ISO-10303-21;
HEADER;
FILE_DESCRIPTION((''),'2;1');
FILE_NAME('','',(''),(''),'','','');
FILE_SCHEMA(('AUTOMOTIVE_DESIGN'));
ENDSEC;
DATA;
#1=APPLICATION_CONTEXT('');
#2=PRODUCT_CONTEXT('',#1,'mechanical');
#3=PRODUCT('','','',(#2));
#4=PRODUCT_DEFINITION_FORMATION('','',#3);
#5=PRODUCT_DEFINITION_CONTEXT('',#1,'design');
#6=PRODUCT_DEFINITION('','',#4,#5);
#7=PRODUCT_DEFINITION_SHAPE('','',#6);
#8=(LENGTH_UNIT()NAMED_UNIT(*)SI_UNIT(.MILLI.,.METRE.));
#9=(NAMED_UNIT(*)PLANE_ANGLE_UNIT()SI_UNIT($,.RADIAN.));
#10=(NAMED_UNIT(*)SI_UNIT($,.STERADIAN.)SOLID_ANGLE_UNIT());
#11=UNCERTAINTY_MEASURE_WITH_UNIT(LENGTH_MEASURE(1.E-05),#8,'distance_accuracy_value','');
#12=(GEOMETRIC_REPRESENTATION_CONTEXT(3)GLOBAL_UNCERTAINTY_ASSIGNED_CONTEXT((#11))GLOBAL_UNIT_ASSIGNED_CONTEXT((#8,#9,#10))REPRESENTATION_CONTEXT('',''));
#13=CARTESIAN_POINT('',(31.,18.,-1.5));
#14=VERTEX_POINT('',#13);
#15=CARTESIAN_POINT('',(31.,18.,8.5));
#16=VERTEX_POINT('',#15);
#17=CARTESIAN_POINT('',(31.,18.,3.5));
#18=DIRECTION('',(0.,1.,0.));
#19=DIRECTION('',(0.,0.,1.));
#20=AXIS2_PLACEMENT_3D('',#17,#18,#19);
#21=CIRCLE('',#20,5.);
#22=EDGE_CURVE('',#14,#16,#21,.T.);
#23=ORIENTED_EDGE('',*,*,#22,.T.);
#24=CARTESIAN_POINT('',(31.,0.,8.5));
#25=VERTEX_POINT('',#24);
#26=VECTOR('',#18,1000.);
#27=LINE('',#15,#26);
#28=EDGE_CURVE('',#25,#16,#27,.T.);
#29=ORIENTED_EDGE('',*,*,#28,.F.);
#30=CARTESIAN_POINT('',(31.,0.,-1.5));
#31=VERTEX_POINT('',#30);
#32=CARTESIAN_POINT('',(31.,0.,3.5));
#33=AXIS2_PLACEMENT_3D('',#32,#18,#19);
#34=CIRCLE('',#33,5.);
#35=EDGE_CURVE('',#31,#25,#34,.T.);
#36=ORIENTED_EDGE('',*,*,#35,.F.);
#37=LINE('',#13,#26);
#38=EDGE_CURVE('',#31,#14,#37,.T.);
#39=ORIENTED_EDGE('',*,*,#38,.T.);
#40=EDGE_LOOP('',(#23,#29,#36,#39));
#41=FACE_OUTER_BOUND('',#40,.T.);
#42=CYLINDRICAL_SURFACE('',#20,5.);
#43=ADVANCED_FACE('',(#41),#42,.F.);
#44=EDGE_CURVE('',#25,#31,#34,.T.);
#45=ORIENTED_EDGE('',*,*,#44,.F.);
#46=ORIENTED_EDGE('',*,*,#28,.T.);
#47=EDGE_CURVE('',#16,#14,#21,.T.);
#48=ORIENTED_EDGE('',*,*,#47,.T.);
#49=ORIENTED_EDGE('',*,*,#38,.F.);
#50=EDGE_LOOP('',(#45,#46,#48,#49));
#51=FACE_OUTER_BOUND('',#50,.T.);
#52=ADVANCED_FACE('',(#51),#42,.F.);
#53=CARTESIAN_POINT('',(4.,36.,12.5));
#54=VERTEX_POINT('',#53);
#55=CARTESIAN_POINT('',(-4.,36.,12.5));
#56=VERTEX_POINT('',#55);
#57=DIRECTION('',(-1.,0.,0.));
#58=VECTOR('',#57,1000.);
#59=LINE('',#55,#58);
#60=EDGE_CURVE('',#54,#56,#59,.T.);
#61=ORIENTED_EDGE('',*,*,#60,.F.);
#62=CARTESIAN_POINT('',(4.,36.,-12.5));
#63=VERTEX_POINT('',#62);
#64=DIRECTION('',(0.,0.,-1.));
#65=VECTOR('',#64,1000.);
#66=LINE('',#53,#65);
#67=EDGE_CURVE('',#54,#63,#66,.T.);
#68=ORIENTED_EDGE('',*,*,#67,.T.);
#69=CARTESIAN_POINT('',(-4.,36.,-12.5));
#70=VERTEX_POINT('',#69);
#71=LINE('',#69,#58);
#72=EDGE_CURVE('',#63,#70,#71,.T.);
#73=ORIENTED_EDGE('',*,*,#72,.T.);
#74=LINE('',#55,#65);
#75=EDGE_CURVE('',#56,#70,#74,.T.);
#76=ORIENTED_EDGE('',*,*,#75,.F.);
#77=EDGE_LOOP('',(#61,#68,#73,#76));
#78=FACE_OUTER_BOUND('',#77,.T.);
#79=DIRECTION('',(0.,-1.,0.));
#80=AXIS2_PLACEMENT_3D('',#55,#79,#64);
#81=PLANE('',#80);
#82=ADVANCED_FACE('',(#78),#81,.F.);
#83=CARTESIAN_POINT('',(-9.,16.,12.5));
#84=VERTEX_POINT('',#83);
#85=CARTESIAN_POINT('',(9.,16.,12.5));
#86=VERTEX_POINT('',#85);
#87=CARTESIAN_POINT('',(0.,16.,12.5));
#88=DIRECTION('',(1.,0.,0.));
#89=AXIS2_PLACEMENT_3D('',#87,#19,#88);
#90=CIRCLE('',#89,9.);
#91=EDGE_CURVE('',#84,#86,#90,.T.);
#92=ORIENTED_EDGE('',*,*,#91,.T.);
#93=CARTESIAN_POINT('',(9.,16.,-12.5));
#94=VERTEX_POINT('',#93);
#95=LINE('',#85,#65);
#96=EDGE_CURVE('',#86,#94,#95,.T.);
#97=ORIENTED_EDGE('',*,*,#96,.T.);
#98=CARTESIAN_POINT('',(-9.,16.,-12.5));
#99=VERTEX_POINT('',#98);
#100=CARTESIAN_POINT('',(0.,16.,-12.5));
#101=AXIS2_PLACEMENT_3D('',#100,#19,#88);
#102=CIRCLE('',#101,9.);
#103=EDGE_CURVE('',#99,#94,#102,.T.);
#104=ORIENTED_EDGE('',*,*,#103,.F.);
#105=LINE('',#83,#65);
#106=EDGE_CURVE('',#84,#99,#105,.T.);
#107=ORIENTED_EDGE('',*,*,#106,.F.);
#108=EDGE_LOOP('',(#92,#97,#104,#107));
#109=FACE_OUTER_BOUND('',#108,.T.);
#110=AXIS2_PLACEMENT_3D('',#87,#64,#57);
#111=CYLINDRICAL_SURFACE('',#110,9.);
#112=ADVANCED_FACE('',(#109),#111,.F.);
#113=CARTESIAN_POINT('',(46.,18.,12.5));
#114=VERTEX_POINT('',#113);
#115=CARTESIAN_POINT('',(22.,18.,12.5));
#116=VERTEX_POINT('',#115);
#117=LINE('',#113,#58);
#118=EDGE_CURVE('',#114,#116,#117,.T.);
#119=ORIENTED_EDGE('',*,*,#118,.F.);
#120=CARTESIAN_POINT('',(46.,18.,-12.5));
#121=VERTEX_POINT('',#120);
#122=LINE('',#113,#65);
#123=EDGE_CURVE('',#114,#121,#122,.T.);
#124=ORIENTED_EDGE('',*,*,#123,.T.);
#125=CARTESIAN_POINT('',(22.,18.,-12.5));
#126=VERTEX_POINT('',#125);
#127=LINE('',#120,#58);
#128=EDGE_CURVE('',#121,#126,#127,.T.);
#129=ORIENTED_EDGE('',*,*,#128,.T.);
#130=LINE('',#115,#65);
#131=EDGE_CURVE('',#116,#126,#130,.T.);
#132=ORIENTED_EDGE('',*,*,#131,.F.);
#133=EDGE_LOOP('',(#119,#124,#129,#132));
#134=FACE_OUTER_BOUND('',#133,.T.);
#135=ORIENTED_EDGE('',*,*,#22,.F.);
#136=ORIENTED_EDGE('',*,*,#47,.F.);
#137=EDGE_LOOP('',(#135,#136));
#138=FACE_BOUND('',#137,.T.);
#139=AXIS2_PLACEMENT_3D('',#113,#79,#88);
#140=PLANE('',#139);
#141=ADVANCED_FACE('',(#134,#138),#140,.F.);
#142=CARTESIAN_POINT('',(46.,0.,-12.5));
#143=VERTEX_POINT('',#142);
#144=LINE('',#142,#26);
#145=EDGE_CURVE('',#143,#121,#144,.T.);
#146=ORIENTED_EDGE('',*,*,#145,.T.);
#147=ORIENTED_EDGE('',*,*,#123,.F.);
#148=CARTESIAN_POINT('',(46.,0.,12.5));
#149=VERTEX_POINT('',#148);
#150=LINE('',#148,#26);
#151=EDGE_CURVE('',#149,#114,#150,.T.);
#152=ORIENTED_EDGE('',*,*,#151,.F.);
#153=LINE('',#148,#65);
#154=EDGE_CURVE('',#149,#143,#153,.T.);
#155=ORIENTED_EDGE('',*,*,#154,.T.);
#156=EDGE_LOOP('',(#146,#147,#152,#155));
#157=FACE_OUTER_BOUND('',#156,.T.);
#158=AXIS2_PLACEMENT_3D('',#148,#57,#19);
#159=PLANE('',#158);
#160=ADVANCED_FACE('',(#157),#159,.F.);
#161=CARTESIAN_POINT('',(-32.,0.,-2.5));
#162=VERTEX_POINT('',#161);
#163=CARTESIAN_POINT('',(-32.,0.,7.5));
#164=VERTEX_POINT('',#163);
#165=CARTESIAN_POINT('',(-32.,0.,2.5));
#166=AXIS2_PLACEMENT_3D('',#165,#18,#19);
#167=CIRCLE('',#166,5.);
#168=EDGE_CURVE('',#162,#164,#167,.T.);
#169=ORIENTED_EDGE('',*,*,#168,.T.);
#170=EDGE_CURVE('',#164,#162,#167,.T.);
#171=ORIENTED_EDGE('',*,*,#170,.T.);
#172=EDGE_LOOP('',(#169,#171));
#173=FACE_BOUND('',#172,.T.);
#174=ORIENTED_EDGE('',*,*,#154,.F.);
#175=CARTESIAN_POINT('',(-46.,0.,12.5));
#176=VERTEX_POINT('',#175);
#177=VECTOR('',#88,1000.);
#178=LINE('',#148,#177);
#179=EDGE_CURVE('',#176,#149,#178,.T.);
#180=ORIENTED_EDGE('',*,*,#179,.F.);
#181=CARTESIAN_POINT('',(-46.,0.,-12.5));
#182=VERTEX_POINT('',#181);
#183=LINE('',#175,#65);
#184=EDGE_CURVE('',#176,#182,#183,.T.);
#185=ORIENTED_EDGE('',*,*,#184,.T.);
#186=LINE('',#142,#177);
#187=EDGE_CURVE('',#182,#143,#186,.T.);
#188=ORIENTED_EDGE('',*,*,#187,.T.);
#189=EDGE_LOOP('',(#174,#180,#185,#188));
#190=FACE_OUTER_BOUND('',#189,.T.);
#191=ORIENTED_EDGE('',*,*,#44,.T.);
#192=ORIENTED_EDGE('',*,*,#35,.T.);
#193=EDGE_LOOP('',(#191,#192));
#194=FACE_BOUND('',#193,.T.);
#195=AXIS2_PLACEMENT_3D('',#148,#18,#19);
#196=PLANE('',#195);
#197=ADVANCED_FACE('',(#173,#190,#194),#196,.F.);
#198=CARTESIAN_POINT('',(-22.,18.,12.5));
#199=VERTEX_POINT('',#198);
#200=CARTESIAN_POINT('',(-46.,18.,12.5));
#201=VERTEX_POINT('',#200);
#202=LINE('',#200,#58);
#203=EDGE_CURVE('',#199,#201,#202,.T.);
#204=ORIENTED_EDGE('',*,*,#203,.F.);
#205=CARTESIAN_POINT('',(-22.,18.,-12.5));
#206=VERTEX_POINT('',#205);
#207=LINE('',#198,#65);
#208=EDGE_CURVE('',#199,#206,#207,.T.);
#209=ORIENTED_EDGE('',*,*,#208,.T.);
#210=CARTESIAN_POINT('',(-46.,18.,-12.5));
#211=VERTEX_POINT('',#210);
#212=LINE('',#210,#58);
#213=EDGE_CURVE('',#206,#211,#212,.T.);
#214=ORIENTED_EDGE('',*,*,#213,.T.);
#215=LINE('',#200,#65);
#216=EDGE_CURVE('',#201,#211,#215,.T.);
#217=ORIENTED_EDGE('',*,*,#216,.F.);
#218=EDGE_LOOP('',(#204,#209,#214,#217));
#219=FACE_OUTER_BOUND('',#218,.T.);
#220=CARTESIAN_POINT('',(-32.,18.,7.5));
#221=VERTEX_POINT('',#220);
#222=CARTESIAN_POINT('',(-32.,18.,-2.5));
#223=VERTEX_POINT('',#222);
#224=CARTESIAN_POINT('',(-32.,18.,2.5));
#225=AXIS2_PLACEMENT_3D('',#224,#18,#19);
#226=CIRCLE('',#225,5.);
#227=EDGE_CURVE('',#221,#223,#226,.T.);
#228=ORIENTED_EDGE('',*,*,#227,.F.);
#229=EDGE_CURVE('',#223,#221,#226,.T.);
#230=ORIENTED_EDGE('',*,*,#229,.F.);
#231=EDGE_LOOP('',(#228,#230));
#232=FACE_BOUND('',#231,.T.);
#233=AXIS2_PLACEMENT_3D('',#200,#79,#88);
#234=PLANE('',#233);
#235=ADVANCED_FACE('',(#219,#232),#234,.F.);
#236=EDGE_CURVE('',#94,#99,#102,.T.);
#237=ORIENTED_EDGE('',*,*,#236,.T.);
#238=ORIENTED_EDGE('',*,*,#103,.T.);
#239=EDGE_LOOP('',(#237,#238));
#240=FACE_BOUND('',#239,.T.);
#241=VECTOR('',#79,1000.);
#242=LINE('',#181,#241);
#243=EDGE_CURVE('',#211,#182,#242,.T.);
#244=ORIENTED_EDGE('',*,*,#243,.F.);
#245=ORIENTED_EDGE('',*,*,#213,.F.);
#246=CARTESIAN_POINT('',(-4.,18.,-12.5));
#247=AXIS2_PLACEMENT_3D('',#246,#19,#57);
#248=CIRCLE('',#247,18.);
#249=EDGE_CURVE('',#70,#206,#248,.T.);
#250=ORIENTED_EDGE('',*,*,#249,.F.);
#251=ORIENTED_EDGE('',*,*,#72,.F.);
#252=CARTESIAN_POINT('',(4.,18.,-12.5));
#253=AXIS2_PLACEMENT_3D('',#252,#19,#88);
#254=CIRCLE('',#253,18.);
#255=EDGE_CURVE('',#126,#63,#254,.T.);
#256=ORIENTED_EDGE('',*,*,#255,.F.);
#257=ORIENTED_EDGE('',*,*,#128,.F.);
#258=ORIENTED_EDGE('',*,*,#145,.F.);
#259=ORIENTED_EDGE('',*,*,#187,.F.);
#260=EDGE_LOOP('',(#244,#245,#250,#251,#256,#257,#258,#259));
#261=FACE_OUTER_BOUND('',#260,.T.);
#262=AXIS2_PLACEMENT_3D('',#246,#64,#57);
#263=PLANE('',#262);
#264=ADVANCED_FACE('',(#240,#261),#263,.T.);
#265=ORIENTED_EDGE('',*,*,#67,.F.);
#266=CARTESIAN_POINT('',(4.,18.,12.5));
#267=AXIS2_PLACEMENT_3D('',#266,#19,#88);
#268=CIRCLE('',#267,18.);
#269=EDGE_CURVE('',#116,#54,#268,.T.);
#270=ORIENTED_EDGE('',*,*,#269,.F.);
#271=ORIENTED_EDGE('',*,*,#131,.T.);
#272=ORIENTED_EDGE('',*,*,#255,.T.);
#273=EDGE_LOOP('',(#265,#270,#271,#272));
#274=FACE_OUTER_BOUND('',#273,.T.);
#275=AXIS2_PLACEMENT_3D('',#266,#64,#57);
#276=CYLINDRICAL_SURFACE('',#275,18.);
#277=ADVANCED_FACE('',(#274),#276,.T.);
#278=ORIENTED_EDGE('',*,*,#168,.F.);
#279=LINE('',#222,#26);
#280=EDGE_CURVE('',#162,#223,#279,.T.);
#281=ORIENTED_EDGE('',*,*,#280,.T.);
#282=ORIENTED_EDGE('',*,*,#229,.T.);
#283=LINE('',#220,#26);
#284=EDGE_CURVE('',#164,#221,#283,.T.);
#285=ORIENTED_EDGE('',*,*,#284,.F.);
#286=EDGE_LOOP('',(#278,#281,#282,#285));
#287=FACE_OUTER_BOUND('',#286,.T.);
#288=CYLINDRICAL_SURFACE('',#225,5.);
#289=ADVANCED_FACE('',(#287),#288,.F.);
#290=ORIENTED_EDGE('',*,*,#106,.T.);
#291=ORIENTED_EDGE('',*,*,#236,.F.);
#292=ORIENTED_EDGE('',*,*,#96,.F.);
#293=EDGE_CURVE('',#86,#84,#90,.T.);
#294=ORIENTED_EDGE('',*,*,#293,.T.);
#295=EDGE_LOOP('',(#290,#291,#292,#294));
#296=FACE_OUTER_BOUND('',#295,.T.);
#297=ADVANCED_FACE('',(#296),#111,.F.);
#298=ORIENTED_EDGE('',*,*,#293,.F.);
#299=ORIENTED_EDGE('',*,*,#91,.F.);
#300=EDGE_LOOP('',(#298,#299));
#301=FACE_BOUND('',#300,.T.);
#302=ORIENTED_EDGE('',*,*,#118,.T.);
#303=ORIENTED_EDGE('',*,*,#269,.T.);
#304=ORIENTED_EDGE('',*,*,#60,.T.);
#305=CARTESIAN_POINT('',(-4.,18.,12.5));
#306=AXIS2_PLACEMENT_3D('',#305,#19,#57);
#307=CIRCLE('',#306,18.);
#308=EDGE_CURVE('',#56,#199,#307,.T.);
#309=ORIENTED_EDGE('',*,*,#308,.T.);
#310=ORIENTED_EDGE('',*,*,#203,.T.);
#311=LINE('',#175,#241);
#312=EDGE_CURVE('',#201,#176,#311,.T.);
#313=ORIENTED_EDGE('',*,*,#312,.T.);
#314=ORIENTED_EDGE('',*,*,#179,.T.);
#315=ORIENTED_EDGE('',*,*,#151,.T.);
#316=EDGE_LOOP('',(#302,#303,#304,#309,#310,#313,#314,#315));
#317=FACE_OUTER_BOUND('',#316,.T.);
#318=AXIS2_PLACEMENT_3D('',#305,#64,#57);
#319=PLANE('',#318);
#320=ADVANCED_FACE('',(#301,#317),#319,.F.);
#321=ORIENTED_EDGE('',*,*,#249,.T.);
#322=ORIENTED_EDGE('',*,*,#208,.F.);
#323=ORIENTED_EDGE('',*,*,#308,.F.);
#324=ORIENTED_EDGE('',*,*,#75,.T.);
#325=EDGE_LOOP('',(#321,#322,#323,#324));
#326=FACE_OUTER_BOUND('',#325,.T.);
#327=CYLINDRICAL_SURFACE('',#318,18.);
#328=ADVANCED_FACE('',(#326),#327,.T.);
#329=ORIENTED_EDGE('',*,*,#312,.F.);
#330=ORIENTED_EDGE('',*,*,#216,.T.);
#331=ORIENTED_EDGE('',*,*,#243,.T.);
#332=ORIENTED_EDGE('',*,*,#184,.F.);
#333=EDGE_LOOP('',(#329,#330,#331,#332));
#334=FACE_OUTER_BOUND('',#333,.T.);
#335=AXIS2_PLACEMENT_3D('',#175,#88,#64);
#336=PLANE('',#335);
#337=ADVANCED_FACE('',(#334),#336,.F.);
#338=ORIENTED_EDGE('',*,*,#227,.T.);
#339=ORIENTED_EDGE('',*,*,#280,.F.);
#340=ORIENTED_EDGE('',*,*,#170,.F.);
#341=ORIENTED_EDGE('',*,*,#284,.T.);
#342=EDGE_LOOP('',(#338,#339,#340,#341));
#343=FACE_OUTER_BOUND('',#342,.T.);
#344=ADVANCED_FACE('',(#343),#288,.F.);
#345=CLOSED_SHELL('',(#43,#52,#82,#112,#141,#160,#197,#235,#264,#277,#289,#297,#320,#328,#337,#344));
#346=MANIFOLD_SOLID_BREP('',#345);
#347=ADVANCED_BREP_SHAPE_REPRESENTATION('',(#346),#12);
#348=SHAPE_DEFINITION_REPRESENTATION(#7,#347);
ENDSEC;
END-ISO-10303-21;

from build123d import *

# Parameters (mm, degrees)
PILLOW_BLOCK_PROFILE_R  = 9
PILLOW_BLOCK_BODY_DEPTH = 12.5
MOUNTING_HOLES_2X_10_D  = 10


with BuildPart() as part:
    # Pillow Block Profile → Pillow Block Body (new, symmetric)
    with BuildSketch(Plane.XY):
        with BuildLine():
            Line((46, 0), (-46, 0))
            Line((-46, 0), (-46, 18))
            Line((-46, 18), (-22, 18))
            ThreePointArc((-22, 18), (-16.727922061, 30.727922061), (-4, 36))
            Line((-4, 36), (4, 36))
            ThreePointArc((4, 36), (16.727922061, 30.727922061), (22, 18))
            Line((22, 18), (46, 18))
            Line((46, 18), (46, 0))
        make_face()
        with Locations((0, 16)):
            Circle(PILLOW_BLOCK_PROFILE_R, mode=Mode.SUBTRACT)
    extrude(amount=PILLOW_BLOCK_BODY_DEPTH, both=True)

    # Mounting Holes 2xØ10 (through all)
    with Locations(Plane(origin=(-32, 18, 2.5), x_dir=(1, 0, 0), z_dir=(0, 1, 0))):
        with Locations((0, 0), (63, -1)):
            Hole(MOUNTING_HOLES_2X_10_D / 2)


solid = part.part
